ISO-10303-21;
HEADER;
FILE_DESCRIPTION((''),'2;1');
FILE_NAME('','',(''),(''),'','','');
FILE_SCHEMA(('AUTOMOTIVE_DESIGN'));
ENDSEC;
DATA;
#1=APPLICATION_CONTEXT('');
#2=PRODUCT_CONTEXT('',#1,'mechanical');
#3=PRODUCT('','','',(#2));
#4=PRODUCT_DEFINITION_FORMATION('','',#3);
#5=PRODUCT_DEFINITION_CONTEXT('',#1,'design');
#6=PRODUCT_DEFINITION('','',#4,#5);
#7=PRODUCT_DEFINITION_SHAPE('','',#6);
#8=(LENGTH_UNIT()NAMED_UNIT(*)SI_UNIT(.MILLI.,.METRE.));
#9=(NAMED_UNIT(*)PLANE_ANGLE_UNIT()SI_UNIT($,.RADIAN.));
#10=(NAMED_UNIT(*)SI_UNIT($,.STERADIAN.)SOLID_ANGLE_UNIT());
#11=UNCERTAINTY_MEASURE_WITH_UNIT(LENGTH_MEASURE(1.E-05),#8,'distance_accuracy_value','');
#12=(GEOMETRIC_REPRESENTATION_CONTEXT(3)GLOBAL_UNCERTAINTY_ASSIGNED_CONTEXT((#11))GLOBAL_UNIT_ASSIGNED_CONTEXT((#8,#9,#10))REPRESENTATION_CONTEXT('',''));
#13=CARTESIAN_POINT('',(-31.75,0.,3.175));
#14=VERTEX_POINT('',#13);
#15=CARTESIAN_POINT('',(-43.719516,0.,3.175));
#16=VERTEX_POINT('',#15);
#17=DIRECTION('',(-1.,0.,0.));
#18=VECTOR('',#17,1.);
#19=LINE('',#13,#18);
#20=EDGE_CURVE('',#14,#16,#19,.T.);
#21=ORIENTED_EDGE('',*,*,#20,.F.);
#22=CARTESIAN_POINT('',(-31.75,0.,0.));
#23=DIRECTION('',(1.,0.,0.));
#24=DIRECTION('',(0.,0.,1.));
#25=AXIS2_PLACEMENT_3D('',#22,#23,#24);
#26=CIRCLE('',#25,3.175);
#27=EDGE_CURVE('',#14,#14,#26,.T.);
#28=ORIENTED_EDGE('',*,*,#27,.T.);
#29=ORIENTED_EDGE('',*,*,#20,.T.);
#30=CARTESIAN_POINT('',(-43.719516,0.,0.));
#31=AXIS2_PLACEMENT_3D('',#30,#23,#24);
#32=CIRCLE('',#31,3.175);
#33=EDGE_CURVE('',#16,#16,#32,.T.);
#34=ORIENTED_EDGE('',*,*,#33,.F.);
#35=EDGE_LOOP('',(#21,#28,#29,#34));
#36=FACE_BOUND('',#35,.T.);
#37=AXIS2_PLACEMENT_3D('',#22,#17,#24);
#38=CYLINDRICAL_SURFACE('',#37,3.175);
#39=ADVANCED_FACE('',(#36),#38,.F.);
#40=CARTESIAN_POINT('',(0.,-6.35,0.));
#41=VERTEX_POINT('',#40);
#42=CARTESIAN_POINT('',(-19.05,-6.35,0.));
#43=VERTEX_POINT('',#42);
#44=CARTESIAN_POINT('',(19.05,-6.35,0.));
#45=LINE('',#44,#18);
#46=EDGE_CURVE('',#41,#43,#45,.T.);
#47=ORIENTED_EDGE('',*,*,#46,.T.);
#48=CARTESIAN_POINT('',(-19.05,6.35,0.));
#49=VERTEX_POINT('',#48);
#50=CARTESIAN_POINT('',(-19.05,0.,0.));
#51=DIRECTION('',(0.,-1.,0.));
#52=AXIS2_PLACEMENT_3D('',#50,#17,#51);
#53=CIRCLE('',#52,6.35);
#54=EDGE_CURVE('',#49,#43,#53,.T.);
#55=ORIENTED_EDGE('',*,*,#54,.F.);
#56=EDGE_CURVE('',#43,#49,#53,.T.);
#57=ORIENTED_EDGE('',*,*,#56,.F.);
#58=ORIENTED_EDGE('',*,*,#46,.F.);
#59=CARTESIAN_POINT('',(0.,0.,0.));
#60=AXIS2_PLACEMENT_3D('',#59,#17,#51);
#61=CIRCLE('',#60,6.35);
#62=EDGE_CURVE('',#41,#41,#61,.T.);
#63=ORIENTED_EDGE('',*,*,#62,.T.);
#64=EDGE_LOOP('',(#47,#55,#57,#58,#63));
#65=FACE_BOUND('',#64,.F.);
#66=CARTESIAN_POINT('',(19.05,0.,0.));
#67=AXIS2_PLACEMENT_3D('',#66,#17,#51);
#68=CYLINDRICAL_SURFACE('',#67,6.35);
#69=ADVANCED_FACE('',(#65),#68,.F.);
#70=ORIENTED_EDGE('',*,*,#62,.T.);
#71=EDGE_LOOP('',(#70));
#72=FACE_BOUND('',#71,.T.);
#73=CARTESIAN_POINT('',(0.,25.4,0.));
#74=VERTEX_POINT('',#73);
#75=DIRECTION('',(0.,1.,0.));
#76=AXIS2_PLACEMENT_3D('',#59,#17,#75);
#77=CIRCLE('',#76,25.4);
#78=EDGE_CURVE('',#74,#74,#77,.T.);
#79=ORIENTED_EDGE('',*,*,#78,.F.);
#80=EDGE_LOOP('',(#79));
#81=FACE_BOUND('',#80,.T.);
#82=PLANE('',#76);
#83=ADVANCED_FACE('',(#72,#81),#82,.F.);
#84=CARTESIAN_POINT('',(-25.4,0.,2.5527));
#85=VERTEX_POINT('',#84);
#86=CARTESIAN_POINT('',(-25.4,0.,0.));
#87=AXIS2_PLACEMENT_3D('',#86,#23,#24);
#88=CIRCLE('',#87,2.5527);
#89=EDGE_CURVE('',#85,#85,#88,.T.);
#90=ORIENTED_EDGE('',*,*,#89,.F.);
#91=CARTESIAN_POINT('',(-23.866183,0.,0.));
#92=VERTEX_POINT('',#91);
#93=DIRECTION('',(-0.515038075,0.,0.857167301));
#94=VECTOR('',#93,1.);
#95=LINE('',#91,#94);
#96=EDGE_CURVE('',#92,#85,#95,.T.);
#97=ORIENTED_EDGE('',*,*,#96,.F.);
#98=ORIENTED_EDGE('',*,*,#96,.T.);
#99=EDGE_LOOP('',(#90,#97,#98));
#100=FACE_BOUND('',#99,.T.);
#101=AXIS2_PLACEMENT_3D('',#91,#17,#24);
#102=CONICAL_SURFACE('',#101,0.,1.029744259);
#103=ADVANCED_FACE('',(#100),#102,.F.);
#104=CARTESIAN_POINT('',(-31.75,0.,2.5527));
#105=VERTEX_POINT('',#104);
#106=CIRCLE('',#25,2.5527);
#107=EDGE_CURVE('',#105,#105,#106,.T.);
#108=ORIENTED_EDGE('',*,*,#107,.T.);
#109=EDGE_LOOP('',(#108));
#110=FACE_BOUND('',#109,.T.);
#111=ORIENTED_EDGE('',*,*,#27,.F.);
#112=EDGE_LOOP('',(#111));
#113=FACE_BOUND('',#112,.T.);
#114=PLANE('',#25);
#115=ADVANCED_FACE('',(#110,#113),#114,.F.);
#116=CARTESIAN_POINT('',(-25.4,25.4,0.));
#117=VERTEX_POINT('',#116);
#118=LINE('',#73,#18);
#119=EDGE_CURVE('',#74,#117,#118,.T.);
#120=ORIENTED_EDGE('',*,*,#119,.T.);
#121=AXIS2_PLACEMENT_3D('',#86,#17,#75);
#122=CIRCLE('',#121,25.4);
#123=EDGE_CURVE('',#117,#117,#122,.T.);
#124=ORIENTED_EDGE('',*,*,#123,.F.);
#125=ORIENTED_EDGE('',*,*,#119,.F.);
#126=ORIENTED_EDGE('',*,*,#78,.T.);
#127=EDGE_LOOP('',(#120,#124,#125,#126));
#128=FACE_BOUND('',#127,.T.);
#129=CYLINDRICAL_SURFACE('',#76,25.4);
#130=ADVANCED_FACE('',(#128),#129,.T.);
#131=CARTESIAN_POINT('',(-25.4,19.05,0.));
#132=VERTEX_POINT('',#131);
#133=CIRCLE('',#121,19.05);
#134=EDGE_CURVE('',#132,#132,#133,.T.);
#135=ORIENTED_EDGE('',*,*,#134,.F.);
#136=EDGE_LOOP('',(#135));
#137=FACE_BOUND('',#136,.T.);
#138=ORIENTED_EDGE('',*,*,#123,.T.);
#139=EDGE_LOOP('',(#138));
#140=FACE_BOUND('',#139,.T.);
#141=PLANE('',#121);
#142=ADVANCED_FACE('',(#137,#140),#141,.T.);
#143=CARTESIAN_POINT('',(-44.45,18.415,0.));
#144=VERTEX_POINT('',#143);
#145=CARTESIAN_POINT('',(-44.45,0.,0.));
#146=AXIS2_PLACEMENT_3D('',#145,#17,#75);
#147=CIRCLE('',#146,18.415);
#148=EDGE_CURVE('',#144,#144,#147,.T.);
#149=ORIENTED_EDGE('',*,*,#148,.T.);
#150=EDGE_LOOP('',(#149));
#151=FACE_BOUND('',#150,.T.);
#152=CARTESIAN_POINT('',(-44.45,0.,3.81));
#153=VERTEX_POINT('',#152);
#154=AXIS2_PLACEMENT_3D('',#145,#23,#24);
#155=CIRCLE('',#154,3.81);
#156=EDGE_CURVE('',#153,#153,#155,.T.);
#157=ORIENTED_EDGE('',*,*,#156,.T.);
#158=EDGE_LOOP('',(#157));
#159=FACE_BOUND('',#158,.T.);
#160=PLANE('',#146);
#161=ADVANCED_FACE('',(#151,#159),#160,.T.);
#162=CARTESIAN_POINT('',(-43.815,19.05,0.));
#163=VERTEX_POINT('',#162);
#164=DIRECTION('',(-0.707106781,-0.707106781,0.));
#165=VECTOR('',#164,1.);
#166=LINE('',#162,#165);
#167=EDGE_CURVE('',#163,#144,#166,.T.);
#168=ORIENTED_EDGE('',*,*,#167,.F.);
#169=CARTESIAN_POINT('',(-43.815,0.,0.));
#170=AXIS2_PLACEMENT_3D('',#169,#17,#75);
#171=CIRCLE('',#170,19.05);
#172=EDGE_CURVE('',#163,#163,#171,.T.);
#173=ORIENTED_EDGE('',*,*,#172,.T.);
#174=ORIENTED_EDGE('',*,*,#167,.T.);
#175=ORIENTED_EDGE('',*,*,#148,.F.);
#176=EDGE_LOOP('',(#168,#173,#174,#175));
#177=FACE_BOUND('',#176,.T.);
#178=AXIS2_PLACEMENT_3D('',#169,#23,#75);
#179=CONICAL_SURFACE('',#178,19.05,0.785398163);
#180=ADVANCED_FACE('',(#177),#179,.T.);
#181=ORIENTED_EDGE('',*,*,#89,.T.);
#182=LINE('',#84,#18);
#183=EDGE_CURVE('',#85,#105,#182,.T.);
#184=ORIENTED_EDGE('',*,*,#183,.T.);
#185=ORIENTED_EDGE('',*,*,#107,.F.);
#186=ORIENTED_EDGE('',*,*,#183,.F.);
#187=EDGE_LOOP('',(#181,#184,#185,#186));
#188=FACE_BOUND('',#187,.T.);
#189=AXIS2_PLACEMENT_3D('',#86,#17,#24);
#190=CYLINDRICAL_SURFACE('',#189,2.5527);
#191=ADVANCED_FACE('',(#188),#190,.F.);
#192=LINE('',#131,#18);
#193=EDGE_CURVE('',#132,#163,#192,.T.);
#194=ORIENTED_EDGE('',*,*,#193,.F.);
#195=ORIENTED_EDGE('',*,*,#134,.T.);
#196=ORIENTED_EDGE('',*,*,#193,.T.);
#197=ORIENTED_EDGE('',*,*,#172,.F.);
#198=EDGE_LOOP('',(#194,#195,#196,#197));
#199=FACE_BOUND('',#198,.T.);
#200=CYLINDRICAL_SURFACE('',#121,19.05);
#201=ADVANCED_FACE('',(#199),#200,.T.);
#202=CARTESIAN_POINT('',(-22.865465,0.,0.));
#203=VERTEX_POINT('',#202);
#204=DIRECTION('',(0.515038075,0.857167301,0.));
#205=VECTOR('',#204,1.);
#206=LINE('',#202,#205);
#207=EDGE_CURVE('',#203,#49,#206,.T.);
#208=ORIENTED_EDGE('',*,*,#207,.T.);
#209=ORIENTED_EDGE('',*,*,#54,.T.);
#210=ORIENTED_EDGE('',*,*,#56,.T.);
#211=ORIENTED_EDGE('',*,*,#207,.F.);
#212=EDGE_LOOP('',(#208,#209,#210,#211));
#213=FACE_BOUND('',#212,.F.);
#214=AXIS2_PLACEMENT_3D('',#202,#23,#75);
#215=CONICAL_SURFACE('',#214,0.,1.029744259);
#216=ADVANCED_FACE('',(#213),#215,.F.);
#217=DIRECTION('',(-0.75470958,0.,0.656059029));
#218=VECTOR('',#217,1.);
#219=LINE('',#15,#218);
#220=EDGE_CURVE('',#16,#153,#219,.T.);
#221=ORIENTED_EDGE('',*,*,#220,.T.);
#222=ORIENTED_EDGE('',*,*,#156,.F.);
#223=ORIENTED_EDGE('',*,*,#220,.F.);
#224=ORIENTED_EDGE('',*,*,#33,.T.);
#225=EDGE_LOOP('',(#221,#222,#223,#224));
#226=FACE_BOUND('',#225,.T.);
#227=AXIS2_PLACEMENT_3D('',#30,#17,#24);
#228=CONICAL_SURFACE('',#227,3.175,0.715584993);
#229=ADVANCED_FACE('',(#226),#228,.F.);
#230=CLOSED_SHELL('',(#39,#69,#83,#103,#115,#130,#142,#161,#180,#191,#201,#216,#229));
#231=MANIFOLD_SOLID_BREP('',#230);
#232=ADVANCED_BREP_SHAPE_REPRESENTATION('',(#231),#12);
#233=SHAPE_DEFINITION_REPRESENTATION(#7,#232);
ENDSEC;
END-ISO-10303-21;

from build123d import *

# Parameters (mm, degrees)
EDGE_CHAMFER_0_025IN_X_45DEG_SIZE  = 0.635
DRILLED_HOLE_0_5_X_0_75_DEEP_D     = 12.7
DRILLED_HOLE_0_5_X_0_75_DEEP_DEPTH = 19.05
DRILLED_HOLE_0_5_X_0_75_DEEP_TIP   = 3.815464931


with BuildPart() as part:
    # Turned Profile Sketch → Turned Body (revolve)
    with BuildSketch(Plane.XY):
        Polygon((0, 0), (0, 25.4), (-25.4, 25.4), (-25.4, 19.05), (-44.45, 19.05), (-44.45, 0), (-0.941021968, 0), align=None)
    revolve(axis=Axis((-0.941021968, 0, 0), (-1, 0, 0)))

    # Sketch4 → Tapped Hole 1-4-20 x 0.5 Deep (revolve, cut)
    with BuildSketch(Plane(origin=(-44.45, 0, 0), x_dir=(0, 0, 1), z_dir=(0, 1, 0))):
        Polygon((0, 0), (0, 20.583816902), (2.5527, 19.05), (2.5527, 12.7), (3.175, 12.7), (3.175, 0.730483939), (3.81, 0), align=None)
    revolve(axis=Axis((-50.8, 0, 0), (1, 0, 0)), mode=Mode.SUBTRACT)

    # Edge Chamfer 0.025in x 45deg
    edge_chamfer_0_025in_x_45deg_edges = [part.edges().sort_by_distance(p)[0] for p in [
        (-44.45, -19.05, 0),
    ]]
    chamfer(edge_chamfer_0_025in_x_45deg_edges, length=EDGE_CHAMFER_0_025IN_X_45DEG_SIZE)

    # Drilled Hole Ø0.5 x 0.75 Deep
    with Locations(Plane.YZ):
        with Locations((0, 0)):
            Hole(DRILLED_HOLE_0_5_X_0_75_DEEP_D / 2, depth=DRILLED_HOLE_0_5_X_0_75_DEEP_DEPTH)
            with Locations((0, 0, -(DRILLED_HOLE_0_5_X_0_75_DEEP_DEPTH + DRILLED_HOLE_0_5_X_0_75_DEEP_TIP / 2))):  # 118° drill point
                Cone(0, DRILLED_HOLE_0_5_X_0_75_DEEP_D / 2, DRILLED_HOLE_0_5_X_0_75_DEEP_TIP, mode=Mode.SUBTRACT)


solid = part.part
